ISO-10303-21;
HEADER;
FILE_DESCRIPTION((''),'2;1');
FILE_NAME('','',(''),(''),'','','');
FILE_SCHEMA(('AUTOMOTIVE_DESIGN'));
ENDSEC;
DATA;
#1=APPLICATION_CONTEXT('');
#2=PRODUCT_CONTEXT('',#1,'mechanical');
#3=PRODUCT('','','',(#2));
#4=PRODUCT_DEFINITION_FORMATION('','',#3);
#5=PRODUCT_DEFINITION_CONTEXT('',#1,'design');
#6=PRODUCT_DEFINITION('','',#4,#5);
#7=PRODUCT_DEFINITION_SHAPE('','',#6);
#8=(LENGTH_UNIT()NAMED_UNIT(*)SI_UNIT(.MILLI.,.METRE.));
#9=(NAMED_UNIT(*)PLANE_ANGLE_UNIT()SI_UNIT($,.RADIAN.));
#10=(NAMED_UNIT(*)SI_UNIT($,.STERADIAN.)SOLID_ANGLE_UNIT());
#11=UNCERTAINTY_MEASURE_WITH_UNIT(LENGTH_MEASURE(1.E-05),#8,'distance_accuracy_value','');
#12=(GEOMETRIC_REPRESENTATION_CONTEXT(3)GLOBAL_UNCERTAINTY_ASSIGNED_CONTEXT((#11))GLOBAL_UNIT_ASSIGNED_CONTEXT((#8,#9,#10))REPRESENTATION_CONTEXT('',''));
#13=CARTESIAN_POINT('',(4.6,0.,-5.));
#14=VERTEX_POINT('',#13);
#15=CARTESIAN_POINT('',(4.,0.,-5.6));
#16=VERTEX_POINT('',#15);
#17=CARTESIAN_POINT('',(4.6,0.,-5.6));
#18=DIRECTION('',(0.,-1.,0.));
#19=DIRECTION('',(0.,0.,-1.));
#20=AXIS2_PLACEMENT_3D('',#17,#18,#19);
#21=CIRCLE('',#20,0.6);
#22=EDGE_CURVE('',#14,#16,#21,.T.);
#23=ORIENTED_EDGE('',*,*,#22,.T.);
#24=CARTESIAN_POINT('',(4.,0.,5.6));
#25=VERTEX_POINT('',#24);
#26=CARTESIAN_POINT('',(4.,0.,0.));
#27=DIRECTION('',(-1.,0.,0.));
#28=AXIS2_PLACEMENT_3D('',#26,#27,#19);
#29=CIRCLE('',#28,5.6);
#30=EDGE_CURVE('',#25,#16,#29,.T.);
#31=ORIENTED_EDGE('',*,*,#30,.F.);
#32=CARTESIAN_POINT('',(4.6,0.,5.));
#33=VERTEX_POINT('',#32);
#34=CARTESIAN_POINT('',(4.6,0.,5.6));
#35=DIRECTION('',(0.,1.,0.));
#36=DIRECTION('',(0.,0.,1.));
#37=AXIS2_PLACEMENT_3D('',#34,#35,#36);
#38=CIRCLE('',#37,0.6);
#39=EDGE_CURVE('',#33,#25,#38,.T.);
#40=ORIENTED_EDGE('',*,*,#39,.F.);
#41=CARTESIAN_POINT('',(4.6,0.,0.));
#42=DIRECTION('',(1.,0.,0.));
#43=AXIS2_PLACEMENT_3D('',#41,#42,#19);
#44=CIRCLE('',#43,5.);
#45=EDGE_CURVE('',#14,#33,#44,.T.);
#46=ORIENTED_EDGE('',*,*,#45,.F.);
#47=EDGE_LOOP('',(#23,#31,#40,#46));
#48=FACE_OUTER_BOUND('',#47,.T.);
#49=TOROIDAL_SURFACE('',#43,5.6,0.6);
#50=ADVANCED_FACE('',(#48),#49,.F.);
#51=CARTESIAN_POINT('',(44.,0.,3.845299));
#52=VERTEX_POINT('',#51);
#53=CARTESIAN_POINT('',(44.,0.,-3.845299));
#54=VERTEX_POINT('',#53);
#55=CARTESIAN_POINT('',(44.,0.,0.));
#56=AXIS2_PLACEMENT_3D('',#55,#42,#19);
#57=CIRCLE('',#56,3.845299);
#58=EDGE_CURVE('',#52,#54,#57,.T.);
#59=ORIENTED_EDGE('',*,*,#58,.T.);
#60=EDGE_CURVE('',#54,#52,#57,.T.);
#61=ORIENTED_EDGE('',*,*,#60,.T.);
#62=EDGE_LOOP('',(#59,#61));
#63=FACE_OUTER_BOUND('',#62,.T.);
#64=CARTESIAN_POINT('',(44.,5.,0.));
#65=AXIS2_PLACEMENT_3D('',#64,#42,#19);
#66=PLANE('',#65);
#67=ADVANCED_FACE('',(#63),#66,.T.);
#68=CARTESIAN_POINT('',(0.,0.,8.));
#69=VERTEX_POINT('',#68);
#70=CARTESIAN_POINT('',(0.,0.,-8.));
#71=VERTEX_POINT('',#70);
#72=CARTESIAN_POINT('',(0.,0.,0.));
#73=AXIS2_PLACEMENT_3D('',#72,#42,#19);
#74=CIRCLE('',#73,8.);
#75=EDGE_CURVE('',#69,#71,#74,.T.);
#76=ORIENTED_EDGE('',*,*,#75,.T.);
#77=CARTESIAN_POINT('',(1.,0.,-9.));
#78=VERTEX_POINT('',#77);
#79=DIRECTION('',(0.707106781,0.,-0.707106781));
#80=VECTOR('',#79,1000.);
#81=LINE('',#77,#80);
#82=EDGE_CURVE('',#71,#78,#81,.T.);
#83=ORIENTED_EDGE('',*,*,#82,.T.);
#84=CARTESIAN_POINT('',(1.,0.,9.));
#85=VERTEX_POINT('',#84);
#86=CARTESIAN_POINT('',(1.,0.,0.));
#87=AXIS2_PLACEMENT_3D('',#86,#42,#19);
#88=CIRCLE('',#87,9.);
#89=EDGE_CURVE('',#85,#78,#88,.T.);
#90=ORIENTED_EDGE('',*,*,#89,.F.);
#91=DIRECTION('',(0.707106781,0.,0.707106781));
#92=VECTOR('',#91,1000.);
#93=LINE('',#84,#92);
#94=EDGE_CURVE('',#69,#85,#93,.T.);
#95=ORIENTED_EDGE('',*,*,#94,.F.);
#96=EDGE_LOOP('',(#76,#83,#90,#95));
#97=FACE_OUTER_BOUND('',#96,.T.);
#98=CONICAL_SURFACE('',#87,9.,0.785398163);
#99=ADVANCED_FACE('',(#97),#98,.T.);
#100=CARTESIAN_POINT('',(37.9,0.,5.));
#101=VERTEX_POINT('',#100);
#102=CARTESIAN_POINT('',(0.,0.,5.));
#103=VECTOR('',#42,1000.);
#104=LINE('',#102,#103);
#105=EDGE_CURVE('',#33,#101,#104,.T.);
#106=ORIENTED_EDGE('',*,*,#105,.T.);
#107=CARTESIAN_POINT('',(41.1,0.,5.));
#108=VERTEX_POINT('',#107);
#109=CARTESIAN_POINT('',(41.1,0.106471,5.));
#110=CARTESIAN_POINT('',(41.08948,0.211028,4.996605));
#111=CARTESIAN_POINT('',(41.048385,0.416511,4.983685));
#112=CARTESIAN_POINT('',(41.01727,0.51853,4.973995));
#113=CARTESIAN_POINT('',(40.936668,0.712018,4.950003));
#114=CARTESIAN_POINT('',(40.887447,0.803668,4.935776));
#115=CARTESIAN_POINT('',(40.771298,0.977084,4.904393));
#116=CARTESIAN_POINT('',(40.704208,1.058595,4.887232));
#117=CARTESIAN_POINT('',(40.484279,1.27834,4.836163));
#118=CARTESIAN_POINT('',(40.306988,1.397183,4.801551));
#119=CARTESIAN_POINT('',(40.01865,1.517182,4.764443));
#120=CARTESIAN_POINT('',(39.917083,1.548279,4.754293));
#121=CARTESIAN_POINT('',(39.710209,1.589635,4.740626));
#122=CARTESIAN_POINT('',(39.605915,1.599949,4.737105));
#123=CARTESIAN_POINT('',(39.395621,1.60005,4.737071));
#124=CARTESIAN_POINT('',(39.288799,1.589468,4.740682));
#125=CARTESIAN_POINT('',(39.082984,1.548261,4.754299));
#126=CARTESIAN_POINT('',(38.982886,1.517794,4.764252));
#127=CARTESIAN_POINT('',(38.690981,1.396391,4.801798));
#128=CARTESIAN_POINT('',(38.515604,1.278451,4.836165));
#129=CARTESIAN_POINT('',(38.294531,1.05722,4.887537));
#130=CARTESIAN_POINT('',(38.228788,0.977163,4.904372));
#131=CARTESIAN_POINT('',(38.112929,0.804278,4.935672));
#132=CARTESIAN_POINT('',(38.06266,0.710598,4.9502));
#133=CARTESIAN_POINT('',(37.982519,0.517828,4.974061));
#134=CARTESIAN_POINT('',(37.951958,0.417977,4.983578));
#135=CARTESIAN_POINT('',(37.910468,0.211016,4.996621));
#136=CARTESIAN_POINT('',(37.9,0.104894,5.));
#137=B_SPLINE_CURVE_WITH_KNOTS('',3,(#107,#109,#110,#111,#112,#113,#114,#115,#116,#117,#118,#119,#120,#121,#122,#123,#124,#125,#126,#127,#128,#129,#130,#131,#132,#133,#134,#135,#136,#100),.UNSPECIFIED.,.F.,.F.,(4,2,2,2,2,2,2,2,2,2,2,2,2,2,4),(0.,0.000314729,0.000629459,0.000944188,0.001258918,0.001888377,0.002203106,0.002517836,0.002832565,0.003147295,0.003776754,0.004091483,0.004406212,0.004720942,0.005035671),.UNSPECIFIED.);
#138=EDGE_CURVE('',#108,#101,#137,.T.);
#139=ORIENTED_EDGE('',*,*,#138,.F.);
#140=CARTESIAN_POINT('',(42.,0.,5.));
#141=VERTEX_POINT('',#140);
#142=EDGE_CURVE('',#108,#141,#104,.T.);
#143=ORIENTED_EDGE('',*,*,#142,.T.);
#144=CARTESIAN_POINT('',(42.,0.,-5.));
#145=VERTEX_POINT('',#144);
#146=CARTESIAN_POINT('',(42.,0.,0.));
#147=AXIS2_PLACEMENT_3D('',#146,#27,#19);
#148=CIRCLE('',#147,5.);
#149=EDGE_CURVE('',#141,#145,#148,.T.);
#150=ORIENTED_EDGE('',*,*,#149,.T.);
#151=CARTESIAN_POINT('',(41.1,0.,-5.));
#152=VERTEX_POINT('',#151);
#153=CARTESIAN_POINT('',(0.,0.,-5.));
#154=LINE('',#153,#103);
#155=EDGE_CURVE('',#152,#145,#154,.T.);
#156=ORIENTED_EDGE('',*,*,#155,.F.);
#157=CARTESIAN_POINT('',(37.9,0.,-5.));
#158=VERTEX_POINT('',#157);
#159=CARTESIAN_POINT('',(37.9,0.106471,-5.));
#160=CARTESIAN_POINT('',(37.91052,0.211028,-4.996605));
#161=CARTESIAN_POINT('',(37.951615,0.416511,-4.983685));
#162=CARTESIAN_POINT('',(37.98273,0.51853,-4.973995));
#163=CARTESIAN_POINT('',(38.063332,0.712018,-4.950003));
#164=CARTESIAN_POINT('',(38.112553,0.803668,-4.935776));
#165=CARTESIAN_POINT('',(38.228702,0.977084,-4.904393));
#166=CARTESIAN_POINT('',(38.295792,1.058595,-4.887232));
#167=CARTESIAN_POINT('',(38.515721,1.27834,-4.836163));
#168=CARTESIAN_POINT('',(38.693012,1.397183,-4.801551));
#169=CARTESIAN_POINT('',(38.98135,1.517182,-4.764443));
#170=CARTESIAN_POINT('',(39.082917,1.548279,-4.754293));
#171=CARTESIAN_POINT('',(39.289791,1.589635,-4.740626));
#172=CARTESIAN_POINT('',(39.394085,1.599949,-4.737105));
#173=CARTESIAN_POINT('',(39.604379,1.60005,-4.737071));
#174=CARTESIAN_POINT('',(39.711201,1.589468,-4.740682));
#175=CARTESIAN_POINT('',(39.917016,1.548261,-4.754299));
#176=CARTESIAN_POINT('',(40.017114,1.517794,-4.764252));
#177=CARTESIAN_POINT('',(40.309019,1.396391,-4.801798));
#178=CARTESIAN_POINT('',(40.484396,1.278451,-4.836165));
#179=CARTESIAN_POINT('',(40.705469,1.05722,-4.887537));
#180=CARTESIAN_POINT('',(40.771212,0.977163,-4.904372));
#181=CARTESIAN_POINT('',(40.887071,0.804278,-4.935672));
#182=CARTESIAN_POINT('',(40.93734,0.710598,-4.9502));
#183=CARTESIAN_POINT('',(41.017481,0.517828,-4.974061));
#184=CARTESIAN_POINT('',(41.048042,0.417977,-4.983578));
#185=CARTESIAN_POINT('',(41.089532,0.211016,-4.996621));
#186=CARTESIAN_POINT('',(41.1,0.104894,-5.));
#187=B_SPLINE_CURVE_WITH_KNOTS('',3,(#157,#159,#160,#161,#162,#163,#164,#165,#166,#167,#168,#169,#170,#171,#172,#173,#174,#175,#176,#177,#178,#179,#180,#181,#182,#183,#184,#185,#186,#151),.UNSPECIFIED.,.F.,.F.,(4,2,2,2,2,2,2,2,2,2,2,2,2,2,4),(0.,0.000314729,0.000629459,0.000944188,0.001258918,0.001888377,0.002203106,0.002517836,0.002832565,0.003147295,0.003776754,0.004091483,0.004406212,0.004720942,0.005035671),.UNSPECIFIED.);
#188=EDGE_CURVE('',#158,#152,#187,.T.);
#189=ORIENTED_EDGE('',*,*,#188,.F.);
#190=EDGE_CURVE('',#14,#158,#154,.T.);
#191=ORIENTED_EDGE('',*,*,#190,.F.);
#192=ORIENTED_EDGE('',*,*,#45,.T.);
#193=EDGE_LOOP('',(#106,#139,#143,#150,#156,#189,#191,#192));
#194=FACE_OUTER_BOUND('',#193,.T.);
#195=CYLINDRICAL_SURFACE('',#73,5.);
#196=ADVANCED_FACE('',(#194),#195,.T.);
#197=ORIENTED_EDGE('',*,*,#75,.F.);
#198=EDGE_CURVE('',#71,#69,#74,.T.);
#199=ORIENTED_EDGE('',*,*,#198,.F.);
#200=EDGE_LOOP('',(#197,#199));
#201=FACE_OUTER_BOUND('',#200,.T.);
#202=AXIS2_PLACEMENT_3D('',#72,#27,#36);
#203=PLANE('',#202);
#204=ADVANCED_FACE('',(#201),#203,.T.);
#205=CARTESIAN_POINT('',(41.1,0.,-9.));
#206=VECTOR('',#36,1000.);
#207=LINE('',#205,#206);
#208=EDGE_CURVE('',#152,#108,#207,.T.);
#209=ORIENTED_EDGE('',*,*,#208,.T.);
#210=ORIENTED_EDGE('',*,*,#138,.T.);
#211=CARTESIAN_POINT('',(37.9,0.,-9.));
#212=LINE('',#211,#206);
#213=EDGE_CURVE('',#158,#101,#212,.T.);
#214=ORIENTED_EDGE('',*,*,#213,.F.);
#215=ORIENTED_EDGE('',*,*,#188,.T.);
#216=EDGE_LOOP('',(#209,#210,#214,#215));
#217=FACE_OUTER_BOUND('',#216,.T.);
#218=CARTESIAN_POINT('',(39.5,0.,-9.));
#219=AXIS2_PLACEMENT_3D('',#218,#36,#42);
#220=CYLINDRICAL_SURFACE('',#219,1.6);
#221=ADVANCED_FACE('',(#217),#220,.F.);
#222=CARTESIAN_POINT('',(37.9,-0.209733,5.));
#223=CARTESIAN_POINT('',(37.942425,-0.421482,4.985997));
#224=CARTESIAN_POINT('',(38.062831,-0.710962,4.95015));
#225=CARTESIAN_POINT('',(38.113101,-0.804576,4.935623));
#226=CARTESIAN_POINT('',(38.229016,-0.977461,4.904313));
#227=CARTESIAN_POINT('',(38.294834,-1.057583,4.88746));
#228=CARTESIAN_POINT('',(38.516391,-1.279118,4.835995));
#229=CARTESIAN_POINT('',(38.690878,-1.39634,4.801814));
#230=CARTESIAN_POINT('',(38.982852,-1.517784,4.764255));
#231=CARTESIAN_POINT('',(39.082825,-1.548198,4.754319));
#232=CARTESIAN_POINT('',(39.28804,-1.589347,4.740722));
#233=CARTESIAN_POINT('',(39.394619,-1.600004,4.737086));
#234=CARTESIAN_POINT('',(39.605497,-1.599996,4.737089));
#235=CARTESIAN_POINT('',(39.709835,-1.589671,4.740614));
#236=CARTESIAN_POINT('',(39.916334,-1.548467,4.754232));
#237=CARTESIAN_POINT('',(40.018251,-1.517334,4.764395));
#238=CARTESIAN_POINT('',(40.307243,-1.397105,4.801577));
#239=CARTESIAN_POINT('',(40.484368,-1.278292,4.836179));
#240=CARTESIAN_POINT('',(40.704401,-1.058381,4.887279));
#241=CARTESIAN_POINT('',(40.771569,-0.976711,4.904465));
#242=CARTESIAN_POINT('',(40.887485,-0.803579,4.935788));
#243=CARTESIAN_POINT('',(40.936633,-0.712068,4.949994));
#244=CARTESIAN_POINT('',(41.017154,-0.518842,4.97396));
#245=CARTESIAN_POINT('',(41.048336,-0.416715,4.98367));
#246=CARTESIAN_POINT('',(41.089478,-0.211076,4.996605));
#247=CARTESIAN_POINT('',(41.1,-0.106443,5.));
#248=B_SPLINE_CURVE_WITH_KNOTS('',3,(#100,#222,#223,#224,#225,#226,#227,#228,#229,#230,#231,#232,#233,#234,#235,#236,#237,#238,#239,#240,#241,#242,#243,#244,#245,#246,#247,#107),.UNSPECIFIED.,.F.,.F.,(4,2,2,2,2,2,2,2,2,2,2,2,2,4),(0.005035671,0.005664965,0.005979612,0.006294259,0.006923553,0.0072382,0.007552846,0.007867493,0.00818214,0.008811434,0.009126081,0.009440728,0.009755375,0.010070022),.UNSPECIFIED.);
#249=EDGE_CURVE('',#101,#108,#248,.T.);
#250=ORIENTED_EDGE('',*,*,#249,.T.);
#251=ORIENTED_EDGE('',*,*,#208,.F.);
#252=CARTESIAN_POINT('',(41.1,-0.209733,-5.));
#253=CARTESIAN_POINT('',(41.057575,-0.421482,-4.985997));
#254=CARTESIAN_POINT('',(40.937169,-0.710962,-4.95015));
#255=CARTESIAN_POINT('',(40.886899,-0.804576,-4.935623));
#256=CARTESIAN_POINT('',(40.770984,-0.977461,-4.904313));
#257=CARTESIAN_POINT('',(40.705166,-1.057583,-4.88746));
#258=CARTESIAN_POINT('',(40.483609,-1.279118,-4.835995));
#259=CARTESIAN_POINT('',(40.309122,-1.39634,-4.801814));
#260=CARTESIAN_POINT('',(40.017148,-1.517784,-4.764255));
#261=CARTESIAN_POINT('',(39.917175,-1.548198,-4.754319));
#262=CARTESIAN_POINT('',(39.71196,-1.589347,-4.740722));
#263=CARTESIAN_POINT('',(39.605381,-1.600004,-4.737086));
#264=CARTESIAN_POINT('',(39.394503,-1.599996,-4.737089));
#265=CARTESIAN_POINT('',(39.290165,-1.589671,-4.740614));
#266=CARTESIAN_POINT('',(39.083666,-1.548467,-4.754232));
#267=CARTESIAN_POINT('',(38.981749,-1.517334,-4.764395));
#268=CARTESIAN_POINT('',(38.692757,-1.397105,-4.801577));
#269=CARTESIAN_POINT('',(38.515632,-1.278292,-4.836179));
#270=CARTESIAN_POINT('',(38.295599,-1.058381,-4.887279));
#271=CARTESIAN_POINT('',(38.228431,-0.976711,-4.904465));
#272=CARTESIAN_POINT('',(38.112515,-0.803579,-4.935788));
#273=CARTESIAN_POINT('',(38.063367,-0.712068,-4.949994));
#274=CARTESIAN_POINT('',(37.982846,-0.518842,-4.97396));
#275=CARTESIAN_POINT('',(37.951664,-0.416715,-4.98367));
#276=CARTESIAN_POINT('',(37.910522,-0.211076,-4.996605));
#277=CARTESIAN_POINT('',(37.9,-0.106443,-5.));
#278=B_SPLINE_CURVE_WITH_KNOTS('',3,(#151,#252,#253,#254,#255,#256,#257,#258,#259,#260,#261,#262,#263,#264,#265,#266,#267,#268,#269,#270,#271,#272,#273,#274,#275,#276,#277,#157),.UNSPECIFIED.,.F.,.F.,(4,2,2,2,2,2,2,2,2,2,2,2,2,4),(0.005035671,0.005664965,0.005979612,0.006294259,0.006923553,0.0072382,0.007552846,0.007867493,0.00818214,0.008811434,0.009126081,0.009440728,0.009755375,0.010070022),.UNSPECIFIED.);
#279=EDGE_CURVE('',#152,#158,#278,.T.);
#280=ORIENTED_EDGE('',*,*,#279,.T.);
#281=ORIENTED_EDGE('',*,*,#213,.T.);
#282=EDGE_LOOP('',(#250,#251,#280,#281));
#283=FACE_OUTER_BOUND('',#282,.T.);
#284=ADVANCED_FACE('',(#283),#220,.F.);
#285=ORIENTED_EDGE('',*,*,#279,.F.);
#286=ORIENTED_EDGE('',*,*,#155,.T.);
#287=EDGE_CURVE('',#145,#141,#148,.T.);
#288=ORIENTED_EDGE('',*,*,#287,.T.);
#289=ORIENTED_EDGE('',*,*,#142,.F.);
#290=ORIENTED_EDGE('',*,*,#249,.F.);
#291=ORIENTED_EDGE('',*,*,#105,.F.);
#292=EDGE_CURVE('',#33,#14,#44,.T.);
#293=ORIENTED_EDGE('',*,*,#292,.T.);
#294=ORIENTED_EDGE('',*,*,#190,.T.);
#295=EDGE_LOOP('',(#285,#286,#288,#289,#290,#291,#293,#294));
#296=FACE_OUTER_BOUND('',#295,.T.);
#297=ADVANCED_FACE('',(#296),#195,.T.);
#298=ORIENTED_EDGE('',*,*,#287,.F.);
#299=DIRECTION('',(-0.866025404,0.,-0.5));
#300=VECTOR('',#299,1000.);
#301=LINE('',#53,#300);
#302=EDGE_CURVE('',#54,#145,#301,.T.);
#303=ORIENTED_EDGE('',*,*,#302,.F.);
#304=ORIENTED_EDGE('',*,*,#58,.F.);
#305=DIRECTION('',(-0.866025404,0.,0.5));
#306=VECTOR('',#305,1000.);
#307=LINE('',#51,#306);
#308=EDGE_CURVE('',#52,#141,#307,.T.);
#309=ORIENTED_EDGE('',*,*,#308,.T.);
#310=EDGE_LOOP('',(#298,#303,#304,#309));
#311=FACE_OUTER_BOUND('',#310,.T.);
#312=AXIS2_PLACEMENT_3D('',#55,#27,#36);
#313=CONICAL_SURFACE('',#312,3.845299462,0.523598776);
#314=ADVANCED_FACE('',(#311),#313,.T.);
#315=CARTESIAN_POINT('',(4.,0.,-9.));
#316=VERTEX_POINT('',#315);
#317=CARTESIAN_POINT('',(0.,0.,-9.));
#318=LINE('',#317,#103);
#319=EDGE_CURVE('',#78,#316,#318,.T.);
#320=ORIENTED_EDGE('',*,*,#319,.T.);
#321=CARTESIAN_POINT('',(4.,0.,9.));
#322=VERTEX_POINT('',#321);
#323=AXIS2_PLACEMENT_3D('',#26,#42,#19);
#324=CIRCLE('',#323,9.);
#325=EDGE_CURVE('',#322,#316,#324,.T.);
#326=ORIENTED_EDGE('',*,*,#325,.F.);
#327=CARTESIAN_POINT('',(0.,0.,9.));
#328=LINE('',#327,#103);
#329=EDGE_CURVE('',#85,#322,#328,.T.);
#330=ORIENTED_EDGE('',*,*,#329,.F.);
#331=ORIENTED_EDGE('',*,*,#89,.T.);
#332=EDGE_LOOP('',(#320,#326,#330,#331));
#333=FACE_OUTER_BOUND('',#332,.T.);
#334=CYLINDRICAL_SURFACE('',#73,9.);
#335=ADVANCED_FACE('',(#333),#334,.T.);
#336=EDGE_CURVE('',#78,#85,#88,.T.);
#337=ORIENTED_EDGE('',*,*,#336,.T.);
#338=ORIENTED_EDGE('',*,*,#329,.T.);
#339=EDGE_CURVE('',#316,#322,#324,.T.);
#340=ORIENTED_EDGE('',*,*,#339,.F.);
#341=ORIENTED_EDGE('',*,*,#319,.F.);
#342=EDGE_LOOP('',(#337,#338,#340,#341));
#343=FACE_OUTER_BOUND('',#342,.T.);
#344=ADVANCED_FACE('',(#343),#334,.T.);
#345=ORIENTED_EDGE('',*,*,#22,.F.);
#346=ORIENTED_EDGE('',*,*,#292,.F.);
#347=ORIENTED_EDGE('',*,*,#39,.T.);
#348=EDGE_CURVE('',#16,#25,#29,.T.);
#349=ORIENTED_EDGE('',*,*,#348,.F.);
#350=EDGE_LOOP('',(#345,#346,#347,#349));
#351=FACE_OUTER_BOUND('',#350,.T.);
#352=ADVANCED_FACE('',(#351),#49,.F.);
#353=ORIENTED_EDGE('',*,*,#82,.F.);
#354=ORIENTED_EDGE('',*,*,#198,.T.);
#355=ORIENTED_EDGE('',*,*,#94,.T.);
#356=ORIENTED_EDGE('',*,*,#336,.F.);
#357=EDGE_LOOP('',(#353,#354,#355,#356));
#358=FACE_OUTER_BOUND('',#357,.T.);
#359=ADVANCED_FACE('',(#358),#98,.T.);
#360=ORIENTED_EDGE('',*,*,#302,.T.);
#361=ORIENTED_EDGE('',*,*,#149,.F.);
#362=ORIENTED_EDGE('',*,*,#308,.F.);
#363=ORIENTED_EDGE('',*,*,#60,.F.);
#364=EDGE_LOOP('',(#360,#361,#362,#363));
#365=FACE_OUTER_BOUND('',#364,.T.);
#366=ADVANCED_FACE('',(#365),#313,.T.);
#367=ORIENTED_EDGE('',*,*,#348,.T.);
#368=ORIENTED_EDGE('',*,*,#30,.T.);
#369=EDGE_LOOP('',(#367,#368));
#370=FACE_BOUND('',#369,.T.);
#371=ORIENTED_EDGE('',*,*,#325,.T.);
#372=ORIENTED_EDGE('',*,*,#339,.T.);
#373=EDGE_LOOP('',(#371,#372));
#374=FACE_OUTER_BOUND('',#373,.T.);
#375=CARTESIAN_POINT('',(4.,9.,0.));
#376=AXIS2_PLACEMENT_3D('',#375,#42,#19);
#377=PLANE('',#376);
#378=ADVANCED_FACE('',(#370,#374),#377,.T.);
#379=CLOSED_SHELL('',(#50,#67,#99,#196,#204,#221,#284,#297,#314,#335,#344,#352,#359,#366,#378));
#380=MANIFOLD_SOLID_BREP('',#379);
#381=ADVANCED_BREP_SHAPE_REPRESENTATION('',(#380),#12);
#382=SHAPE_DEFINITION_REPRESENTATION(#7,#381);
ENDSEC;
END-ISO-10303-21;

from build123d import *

# Parameters (mm, degrees)
CUT_EXTRUDE1_DEPTH      = 46.803929962
CUT_EXTRUDE1_DEPTH_BACK = 46.803929962
SKETCH2_R               = 1.6
FILLET1_R               = 0.6
CHAMFER1_SIZE           = 2
CHAMFER1_SIZE2          = 1.154700538


with BuildPart() as part:
    # Sketch1 → Base-Revolve (revolve)
    with BuildSketch(Plane.XY, mode=Mode.PRIVATE) as base_revolve_sk:
        Polygon((0, 0), (44, 0), (44, 5), (4, 5), (4, 9), (1, 9), (0, 8), align=None)
    revolve(base_revolve_sk.sketch.rotate(Axis((0, 0, 0), (-1, 0, 0)), 90), axis=Axis((0, 0, 0), (-1, 0, 0)))

    # Sketch2 → Cut-Extrude1 (cut, two sides: drawn at the far end of the back side and taken through both)
    with BuildSketch(Plane.XY.offset(-CUT_EXTRUDE1_DEPTH_BACK)):
        with Locations((39.5, 0)):
            Circle(SKETCH2_R)
    extrude(amount=CUT_EXTRUDE1_DEPTH + CUT_EXTRUDE1_DEPTH_BACK, mode=Mode.SUBTRACT)

    # Fillet1
    fillet1_edges = [part.edges().sort_by_distance(p)[0] for p in [
        (4, 0, 5),
    ]]
    fillet(fillet1_edges, radius=FILLET1_R)

    # Chamfer1
    chamfer1_edges = [part.edges().sort_by_distance(p)[0] for p in [
        (44, 0, 5),
    ]]
    chamfer1_side = [part.faces().sort_by_distance(p)[0] for p in [
        (24.3, 0, 5),
    ]]
    chamfer(chamfer1_edges, length=CHAMFER1_SIZE, length2=CHAMFER1_SIZE2, reference=chamfer1_side[0])


solid = part.part
